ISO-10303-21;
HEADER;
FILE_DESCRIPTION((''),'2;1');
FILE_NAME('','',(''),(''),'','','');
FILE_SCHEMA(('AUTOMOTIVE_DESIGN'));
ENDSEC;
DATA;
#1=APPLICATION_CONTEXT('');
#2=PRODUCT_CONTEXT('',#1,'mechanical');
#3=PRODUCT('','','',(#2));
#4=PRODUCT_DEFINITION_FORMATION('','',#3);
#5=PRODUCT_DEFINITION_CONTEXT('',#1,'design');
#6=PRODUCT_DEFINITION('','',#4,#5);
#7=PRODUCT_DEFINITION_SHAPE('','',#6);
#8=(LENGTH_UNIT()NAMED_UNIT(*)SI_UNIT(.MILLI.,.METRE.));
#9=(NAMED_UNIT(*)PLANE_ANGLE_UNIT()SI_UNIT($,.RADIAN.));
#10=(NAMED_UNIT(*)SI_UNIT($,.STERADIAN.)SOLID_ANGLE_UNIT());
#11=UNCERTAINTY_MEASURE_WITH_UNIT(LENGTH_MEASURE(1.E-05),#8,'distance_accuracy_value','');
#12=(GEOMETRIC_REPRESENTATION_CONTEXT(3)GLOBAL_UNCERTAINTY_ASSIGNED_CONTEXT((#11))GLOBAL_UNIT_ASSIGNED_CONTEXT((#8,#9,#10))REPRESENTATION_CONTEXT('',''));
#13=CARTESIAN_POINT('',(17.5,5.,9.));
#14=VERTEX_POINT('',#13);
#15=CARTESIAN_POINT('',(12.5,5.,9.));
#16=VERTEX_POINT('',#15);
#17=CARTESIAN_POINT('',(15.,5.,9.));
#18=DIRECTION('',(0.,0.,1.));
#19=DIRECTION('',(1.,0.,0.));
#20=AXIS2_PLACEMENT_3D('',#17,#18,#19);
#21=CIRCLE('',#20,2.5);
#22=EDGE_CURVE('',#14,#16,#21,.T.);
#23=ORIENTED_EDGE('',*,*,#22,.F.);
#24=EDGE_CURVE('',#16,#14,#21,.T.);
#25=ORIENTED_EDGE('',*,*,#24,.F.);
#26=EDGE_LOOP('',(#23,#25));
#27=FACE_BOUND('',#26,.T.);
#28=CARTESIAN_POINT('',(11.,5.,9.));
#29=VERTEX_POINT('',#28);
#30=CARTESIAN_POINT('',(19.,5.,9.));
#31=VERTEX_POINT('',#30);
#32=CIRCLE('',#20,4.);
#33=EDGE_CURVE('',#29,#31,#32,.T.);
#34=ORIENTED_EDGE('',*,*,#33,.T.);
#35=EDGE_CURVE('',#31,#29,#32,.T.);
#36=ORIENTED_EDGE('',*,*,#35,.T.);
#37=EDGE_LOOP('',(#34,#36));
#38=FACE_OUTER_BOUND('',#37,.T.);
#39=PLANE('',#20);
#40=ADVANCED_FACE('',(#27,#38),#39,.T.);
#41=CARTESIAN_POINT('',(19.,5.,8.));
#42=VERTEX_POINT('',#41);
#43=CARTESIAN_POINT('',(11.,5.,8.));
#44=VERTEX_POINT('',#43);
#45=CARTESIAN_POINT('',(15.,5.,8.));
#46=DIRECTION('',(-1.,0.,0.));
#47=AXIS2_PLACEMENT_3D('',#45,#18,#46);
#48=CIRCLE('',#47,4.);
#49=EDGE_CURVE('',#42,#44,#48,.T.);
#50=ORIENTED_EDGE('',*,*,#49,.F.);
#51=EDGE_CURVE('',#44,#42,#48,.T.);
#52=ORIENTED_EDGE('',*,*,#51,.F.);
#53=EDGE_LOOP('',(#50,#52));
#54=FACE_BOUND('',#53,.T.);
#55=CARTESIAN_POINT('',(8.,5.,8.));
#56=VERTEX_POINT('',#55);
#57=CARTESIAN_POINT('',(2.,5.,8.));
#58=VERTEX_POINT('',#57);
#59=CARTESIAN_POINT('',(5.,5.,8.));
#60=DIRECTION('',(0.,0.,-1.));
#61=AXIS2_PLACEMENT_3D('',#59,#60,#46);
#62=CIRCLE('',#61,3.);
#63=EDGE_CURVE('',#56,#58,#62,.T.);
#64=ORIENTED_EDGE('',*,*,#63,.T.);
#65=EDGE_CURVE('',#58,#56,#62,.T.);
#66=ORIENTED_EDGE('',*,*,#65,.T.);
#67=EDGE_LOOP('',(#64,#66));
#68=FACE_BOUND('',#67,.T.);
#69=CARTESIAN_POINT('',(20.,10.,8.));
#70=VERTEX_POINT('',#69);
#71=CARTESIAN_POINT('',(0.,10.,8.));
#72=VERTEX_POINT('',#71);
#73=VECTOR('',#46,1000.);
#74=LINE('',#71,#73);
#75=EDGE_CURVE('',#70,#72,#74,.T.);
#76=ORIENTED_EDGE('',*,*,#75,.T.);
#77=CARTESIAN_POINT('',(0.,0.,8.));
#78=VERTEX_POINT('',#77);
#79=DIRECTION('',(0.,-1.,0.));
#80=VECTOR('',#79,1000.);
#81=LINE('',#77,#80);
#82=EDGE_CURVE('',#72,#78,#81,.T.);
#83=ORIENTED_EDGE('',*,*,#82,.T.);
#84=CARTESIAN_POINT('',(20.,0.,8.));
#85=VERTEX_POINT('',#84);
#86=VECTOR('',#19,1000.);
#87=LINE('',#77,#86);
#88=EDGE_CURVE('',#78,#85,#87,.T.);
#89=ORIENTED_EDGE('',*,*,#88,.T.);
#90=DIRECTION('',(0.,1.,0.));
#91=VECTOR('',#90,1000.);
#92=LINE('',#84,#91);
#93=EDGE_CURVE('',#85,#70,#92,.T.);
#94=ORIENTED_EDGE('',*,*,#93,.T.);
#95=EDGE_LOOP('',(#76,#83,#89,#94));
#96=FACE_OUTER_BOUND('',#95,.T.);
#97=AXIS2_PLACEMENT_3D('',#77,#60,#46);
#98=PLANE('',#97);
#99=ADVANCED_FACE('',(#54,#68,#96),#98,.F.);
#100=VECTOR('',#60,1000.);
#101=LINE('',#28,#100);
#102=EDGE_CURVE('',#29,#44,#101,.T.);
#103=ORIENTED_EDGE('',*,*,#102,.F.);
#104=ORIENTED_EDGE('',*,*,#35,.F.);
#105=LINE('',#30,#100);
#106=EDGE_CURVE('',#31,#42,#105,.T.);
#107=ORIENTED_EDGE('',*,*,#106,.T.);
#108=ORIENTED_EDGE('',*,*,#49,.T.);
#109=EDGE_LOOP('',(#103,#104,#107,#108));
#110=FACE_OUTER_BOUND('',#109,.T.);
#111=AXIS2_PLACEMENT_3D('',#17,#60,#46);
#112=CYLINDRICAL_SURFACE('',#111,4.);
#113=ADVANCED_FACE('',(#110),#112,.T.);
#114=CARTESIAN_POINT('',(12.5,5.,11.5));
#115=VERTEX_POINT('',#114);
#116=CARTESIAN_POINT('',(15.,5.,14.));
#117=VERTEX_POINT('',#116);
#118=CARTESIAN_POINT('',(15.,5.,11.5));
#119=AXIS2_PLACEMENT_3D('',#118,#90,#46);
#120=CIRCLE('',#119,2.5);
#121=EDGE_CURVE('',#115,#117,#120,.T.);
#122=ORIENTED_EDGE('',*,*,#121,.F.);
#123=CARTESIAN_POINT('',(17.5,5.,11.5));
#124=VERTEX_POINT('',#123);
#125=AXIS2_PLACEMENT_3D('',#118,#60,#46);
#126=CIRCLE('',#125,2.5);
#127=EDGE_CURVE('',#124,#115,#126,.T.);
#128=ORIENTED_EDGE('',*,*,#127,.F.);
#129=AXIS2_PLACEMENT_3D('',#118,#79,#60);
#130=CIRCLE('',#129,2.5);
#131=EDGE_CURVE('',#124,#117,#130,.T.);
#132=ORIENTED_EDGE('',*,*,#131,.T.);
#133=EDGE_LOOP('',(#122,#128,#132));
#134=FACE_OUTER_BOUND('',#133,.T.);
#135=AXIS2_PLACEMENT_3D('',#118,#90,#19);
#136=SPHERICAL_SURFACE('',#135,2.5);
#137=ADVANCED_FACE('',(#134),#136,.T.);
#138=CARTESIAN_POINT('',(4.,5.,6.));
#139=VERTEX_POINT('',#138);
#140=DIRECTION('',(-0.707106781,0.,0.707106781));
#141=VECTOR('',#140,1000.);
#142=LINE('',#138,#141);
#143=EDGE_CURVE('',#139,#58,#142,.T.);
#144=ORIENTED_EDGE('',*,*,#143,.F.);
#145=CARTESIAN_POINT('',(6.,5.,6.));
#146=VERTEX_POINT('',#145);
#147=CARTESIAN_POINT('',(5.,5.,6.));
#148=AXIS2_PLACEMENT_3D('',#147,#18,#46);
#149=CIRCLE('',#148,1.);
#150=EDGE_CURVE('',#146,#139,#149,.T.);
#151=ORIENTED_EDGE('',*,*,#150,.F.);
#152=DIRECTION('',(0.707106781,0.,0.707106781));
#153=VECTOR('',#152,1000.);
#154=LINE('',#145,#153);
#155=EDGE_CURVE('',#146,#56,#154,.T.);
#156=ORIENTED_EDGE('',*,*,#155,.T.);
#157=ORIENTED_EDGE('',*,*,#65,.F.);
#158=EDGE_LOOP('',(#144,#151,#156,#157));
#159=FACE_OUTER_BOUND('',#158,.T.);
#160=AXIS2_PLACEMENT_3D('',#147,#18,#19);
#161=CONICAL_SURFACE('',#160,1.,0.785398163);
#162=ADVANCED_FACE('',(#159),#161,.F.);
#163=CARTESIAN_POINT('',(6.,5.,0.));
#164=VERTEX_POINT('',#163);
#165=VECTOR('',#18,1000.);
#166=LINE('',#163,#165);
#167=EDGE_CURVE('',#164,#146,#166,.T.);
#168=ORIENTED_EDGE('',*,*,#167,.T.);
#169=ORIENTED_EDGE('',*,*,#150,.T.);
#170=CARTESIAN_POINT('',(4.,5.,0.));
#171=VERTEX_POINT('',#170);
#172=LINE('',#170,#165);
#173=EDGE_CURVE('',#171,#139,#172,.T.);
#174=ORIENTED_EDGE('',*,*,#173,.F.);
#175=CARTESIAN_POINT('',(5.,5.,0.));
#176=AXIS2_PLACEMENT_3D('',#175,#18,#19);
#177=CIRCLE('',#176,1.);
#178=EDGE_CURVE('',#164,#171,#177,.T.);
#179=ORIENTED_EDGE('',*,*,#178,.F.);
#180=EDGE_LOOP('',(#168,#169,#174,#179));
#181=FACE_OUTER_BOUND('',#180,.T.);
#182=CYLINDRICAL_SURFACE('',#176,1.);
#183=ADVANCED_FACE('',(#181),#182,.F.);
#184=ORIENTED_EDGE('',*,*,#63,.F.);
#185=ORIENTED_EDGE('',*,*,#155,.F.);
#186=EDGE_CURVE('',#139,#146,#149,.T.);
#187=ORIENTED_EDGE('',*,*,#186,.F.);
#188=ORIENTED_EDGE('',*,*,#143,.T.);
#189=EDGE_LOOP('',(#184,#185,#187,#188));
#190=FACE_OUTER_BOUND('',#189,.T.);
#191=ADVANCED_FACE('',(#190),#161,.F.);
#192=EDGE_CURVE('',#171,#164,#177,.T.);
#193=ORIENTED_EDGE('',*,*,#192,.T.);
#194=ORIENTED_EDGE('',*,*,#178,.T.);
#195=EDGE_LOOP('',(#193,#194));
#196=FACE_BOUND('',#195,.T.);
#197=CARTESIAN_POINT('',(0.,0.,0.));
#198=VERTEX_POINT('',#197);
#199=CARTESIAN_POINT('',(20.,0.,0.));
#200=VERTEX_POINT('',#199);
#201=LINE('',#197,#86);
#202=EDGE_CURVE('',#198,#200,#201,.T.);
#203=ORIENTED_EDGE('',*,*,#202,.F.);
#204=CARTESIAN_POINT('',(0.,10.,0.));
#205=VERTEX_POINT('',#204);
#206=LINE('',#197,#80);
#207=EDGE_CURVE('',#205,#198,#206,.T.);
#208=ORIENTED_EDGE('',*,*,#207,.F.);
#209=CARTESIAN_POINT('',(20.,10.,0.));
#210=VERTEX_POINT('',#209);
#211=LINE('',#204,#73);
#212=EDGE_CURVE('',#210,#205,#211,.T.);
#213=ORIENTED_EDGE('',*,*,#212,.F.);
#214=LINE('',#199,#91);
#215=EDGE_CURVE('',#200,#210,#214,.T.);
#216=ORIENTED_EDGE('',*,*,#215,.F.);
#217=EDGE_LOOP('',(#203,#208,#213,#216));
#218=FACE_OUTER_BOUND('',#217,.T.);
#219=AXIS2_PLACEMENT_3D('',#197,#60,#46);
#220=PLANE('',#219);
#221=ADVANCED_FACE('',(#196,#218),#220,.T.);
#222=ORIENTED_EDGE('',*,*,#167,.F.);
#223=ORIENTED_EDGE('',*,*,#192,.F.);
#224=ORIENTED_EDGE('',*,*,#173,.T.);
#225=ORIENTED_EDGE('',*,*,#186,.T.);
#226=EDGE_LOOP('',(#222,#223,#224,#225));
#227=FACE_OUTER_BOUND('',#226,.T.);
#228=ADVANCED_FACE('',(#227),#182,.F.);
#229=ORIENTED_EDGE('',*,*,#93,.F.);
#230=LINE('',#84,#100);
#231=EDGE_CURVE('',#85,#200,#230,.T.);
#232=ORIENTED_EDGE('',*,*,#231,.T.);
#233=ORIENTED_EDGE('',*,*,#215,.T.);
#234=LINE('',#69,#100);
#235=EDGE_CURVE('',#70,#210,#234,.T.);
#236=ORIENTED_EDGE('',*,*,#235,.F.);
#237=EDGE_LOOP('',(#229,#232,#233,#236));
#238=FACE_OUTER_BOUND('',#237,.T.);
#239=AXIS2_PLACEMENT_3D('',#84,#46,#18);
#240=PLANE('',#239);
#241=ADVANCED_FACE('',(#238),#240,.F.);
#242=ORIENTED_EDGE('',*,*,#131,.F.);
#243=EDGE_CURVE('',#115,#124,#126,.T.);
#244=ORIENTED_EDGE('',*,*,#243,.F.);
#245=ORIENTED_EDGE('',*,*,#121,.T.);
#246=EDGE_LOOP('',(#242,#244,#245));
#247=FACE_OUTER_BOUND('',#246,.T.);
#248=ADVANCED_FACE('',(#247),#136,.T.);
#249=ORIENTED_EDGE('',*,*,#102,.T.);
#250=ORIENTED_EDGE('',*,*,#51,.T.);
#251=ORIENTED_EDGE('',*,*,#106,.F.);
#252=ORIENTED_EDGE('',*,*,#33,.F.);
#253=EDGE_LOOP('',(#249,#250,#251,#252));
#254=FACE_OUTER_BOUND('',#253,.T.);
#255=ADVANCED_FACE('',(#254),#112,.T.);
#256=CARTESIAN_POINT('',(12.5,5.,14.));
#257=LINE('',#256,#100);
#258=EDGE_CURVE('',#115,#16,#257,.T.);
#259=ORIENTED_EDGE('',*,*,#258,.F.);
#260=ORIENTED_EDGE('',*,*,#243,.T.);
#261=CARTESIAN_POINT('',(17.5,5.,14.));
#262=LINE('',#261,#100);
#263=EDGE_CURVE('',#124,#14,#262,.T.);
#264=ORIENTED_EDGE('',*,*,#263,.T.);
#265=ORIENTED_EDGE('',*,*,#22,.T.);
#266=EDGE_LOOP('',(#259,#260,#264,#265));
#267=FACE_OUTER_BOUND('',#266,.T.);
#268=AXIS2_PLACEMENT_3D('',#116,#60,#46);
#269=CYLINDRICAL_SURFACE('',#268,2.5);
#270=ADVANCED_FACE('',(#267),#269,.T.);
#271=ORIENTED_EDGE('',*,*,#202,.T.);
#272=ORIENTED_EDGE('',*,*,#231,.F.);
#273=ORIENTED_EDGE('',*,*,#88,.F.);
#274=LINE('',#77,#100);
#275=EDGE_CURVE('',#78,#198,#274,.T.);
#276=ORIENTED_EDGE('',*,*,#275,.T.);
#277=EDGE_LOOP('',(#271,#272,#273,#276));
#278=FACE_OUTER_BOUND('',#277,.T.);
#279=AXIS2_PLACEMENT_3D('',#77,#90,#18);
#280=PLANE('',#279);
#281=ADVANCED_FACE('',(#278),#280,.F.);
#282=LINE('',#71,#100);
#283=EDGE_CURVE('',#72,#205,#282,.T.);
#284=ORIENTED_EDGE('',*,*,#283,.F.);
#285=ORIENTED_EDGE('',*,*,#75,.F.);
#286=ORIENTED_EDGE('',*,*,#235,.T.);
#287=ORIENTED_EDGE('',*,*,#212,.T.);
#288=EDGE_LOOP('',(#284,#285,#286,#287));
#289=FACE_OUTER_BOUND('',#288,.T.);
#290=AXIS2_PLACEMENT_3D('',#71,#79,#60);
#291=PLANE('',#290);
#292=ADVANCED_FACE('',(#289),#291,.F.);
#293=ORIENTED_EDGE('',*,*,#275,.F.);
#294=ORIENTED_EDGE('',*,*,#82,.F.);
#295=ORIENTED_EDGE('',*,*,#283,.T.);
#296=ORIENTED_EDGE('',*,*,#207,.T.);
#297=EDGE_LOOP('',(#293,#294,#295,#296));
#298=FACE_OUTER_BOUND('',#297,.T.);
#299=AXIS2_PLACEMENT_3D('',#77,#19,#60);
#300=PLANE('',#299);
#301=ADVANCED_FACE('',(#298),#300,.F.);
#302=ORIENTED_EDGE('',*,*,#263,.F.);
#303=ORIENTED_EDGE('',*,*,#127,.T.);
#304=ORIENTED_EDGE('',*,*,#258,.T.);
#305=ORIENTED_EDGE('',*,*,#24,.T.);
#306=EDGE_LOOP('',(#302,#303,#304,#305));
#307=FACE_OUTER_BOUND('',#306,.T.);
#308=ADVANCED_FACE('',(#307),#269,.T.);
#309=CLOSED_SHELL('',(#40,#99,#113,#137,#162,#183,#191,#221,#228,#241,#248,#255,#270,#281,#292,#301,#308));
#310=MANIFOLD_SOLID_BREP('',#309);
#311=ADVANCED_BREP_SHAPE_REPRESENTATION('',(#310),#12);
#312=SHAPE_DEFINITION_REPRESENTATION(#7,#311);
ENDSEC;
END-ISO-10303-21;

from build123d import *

# Parameters (mm, degrees)
SKETCH_1_W          = 20
SKETCH_1_H          = 10
EXTRUDE_1_DEPTH     = 8
SKETCH_2_R          = 1
CUT_EXTRUDE_1_DEPTH = 8
CHAMFER_1_SIZE      = 2
SKETCH_3_R          = 4
EXTRUDE_2_DEPTH     = 1
SKETCH_4_R          = 2.5
EXTRUDE_3_DEPTH     = 5
FILLET_1_R          = 2.5


with BuildPart() as part:
    # 草图1 → 凸台-拉伸1 (new body)
    with BuildSketch(Plane.XY):
        with Locations((10, 5)):
            Rectangle(SKETCH_1_W, SKETCH_1_H)
    extrude(amount=EXTRUDE_1_DEPTH)

    # 草图2 → 切除-拉伸1 (cut)
    with BuildSketch(Plane.XY.offset(8)):
        with Locations((5, 5)):
            Circle(SKETCH_2_R)
    extrude(amount=-CUT_EXTRUDE_1_DEPTH, mode=Mode.SUBTRACT)

    # 倒角1
    chamfer_1_edges = [part.edges().sort_by_distance(p)[0] for p in [
        (4, 5, 8),
    ]]
    chamfer(chamfer_1_edges, length=CHAMFER_1_SIZE)

    # 草图3 → 凸台-拉伸2 (add)
    with BuildSketch(Plane.XY.offset(8)):
        with Locations(Location((15, 5, 0), (0, 0, 180))):
            Circle(SKETCH_3_R)
    extrude(amount=EXTRUDE_2_DEPTH)

    # 草图4 → 凸台-拉伸3 (add)
    with BuildSketch(Plane.XY.offset(9)):
        with Locations((15, 5)):
            Circle(SKETCH_4_R)
    extrude(amount=EXTRUDE_3_DEPTH)

    # 圆角1
    fillet_1_edges = [part.edges().sort_by_distance(p)[0] for p in [
        (12.5, 5, 14),
    ]]
    fillet(fillet_1_edges, radius=FILLET_1_R)


solid = part.part
